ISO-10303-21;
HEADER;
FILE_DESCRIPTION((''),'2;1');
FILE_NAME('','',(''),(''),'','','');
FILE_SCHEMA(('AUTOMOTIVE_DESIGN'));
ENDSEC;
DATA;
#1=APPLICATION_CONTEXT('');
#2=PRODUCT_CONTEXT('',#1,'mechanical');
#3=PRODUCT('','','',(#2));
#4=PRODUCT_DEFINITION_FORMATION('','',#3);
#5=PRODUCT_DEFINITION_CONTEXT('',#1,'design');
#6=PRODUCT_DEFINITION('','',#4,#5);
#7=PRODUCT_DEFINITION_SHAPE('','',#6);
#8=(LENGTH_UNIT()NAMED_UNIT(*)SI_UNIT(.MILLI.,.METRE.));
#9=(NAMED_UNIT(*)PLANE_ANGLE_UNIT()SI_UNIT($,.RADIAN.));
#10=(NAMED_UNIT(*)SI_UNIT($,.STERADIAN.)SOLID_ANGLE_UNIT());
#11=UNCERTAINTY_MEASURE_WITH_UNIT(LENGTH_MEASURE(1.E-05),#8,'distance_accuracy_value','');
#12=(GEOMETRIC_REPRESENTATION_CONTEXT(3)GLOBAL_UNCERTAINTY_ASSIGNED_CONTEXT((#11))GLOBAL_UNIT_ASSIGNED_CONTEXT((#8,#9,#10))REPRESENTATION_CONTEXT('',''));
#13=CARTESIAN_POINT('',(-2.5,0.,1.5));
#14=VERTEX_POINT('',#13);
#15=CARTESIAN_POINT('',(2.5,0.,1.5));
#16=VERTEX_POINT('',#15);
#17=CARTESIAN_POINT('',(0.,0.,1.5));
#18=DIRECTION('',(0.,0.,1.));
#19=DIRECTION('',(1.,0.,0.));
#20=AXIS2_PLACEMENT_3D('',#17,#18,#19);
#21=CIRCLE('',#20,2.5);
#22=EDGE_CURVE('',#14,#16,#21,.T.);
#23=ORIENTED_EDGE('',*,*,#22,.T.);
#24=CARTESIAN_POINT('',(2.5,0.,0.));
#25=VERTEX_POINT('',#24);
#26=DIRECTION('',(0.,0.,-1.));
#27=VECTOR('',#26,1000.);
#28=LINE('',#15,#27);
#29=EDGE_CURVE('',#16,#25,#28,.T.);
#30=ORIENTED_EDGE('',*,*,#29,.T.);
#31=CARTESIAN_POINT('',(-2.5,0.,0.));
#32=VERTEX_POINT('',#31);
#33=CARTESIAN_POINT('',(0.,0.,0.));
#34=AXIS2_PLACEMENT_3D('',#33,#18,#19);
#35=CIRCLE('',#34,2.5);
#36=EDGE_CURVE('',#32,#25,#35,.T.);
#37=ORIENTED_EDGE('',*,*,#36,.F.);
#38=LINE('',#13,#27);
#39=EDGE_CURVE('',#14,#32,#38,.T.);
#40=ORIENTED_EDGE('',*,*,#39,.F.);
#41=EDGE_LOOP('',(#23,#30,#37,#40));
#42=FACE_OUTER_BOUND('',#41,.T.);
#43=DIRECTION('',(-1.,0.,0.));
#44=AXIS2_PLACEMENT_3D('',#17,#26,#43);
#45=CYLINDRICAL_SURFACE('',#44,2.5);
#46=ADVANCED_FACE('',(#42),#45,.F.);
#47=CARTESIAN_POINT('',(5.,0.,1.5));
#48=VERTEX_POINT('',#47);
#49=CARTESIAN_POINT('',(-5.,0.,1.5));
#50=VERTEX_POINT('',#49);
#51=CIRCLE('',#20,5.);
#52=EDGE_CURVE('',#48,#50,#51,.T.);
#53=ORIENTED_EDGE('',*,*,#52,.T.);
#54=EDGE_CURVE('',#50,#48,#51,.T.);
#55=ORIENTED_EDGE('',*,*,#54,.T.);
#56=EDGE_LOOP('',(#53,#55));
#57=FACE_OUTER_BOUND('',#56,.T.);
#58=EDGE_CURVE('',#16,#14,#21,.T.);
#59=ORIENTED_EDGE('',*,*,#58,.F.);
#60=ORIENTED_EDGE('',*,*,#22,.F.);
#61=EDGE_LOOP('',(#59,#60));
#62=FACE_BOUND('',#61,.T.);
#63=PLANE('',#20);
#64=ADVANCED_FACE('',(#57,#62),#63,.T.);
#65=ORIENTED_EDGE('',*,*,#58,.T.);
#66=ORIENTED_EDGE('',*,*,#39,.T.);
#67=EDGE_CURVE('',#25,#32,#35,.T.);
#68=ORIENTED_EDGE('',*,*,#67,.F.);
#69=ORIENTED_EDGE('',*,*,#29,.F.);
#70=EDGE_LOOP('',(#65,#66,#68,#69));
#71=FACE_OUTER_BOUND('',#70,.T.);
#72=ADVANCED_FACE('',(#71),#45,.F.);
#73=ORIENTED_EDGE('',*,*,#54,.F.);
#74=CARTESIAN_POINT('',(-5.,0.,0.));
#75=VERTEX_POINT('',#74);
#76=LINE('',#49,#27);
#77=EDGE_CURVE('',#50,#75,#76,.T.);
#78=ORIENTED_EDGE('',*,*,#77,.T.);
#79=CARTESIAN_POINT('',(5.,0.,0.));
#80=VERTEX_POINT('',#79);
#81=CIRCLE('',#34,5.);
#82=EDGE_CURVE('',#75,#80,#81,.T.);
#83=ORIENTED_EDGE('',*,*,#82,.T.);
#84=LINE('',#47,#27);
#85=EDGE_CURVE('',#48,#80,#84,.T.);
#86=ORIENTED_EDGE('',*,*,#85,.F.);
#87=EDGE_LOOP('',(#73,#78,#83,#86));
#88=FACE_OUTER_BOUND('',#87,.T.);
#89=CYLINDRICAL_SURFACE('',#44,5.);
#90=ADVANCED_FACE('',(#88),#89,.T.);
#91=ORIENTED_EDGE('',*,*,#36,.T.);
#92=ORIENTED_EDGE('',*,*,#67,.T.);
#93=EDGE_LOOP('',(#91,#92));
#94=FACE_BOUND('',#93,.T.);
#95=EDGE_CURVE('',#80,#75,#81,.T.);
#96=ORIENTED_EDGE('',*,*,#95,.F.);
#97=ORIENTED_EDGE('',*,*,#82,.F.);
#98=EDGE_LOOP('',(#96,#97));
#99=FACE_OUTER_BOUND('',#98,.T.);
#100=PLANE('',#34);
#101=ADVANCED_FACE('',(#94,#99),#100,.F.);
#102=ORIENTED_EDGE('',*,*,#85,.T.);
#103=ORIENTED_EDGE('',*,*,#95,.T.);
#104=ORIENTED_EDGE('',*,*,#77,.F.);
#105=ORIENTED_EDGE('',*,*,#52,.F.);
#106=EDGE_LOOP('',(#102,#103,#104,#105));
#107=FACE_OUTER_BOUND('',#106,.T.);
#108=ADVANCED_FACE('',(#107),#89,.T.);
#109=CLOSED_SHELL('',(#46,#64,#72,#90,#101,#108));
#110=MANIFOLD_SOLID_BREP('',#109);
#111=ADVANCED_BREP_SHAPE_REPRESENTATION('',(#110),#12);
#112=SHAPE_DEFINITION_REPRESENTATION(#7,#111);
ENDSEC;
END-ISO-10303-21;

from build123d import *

# Parameters (mm, degrees)
SKETCH1_R           = 5
SKETCH1_R_2         = 2.5
BOSS_EXTRUDE1_DEPTH = 1.5


with BuildPart() as part:
    # Sketch1 → Boss-Extrude1 (new body)
    with BuildSketch(Plane.XY):
        Circle(SKETCH1_R)
        Circle(SKETCH1_R_2, mode=Mode.SUBTRACT)
    extrude(amount=BOSS_EXTRUDE1_DEPTH)


solid = part.part
